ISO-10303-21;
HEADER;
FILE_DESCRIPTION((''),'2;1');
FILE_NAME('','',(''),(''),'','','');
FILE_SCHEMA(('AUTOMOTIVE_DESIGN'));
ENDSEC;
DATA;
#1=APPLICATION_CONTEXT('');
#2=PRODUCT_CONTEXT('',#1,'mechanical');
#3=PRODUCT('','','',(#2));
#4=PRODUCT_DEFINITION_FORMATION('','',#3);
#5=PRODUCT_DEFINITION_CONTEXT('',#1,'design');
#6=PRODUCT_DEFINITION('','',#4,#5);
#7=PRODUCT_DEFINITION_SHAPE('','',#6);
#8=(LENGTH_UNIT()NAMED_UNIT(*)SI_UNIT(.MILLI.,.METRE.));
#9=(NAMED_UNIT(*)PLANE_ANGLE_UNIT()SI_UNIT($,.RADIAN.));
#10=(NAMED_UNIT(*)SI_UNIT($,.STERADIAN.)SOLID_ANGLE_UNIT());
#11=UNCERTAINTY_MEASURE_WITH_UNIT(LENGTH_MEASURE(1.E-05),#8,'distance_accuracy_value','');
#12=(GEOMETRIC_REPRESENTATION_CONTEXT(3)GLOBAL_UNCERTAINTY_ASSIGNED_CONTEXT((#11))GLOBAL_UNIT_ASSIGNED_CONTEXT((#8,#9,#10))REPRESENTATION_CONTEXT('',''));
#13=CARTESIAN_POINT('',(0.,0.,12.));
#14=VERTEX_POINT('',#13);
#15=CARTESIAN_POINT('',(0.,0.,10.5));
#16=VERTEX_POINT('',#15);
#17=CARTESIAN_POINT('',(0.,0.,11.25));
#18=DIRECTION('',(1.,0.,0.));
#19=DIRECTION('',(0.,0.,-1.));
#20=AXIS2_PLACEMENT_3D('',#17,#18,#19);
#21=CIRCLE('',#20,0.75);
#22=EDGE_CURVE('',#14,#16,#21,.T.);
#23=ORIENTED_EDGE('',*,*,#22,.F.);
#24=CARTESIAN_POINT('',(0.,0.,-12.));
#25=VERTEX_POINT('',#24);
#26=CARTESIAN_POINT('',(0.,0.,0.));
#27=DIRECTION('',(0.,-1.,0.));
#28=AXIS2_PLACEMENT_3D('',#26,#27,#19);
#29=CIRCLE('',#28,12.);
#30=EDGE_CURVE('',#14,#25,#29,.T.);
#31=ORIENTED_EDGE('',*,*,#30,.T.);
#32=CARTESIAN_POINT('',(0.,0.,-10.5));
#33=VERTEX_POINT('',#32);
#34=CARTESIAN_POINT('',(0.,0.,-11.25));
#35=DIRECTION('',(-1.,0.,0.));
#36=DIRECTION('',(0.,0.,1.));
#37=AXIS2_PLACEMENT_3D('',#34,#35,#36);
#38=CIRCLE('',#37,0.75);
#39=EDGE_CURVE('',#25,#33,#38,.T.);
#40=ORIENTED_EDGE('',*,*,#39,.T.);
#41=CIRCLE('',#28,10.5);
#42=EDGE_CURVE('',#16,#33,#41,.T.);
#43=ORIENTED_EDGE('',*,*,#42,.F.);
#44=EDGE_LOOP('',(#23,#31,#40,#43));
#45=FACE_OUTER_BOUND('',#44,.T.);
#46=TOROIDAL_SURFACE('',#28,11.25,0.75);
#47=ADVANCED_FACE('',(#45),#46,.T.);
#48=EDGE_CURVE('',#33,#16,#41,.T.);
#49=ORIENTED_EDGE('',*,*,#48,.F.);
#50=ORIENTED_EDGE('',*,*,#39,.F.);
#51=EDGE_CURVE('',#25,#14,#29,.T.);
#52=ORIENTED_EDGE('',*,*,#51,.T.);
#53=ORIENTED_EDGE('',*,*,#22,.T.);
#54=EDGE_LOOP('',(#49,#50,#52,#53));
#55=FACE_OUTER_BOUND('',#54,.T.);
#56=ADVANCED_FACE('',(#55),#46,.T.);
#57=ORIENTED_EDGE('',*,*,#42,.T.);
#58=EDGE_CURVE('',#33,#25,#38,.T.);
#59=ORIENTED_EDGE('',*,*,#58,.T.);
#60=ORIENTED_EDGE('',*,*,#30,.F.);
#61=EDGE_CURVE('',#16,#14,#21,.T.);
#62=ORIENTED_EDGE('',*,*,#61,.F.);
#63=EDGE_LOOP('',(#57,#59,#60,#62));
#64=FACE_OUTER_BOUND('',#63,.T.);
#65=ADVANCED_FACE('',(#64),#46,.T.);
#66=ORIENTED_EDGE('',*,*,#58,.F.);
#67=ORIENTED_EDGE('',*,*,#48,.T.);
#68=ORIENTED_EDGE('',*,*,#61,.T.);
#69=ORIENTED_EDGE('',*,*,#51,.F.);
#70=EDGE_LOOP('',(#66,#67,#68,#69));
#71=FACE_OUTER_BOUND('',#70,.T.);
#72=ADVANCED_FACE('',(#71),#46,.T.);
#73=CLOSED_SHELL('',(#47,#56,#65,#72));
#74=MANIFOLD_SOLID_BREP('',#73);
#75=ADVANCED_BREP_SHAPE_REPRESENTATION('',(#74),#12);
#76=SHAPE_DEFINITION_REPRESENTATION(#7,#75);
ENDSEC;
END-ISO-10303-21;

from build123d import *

# Parameters (mm, degrees)
SKETCH_1_R = 0.75


with BuildPart() as part:
    # 草图1 → 旋转1 (revolve)
    with BuildSketch(Plane.XY, mode=Mode.PRIVATE) as revolve_1_sk:
        with Locations((-11.25, 0)):
            Circle(SKETCH_1_R)
    revolve(revolve_1_sk.sketch.rotate(Axis((0, 0, 0), (0, 1, 0)), 270), axis=Axis((0, 0, 0), (0, 1, 0)))


solid = part.part
